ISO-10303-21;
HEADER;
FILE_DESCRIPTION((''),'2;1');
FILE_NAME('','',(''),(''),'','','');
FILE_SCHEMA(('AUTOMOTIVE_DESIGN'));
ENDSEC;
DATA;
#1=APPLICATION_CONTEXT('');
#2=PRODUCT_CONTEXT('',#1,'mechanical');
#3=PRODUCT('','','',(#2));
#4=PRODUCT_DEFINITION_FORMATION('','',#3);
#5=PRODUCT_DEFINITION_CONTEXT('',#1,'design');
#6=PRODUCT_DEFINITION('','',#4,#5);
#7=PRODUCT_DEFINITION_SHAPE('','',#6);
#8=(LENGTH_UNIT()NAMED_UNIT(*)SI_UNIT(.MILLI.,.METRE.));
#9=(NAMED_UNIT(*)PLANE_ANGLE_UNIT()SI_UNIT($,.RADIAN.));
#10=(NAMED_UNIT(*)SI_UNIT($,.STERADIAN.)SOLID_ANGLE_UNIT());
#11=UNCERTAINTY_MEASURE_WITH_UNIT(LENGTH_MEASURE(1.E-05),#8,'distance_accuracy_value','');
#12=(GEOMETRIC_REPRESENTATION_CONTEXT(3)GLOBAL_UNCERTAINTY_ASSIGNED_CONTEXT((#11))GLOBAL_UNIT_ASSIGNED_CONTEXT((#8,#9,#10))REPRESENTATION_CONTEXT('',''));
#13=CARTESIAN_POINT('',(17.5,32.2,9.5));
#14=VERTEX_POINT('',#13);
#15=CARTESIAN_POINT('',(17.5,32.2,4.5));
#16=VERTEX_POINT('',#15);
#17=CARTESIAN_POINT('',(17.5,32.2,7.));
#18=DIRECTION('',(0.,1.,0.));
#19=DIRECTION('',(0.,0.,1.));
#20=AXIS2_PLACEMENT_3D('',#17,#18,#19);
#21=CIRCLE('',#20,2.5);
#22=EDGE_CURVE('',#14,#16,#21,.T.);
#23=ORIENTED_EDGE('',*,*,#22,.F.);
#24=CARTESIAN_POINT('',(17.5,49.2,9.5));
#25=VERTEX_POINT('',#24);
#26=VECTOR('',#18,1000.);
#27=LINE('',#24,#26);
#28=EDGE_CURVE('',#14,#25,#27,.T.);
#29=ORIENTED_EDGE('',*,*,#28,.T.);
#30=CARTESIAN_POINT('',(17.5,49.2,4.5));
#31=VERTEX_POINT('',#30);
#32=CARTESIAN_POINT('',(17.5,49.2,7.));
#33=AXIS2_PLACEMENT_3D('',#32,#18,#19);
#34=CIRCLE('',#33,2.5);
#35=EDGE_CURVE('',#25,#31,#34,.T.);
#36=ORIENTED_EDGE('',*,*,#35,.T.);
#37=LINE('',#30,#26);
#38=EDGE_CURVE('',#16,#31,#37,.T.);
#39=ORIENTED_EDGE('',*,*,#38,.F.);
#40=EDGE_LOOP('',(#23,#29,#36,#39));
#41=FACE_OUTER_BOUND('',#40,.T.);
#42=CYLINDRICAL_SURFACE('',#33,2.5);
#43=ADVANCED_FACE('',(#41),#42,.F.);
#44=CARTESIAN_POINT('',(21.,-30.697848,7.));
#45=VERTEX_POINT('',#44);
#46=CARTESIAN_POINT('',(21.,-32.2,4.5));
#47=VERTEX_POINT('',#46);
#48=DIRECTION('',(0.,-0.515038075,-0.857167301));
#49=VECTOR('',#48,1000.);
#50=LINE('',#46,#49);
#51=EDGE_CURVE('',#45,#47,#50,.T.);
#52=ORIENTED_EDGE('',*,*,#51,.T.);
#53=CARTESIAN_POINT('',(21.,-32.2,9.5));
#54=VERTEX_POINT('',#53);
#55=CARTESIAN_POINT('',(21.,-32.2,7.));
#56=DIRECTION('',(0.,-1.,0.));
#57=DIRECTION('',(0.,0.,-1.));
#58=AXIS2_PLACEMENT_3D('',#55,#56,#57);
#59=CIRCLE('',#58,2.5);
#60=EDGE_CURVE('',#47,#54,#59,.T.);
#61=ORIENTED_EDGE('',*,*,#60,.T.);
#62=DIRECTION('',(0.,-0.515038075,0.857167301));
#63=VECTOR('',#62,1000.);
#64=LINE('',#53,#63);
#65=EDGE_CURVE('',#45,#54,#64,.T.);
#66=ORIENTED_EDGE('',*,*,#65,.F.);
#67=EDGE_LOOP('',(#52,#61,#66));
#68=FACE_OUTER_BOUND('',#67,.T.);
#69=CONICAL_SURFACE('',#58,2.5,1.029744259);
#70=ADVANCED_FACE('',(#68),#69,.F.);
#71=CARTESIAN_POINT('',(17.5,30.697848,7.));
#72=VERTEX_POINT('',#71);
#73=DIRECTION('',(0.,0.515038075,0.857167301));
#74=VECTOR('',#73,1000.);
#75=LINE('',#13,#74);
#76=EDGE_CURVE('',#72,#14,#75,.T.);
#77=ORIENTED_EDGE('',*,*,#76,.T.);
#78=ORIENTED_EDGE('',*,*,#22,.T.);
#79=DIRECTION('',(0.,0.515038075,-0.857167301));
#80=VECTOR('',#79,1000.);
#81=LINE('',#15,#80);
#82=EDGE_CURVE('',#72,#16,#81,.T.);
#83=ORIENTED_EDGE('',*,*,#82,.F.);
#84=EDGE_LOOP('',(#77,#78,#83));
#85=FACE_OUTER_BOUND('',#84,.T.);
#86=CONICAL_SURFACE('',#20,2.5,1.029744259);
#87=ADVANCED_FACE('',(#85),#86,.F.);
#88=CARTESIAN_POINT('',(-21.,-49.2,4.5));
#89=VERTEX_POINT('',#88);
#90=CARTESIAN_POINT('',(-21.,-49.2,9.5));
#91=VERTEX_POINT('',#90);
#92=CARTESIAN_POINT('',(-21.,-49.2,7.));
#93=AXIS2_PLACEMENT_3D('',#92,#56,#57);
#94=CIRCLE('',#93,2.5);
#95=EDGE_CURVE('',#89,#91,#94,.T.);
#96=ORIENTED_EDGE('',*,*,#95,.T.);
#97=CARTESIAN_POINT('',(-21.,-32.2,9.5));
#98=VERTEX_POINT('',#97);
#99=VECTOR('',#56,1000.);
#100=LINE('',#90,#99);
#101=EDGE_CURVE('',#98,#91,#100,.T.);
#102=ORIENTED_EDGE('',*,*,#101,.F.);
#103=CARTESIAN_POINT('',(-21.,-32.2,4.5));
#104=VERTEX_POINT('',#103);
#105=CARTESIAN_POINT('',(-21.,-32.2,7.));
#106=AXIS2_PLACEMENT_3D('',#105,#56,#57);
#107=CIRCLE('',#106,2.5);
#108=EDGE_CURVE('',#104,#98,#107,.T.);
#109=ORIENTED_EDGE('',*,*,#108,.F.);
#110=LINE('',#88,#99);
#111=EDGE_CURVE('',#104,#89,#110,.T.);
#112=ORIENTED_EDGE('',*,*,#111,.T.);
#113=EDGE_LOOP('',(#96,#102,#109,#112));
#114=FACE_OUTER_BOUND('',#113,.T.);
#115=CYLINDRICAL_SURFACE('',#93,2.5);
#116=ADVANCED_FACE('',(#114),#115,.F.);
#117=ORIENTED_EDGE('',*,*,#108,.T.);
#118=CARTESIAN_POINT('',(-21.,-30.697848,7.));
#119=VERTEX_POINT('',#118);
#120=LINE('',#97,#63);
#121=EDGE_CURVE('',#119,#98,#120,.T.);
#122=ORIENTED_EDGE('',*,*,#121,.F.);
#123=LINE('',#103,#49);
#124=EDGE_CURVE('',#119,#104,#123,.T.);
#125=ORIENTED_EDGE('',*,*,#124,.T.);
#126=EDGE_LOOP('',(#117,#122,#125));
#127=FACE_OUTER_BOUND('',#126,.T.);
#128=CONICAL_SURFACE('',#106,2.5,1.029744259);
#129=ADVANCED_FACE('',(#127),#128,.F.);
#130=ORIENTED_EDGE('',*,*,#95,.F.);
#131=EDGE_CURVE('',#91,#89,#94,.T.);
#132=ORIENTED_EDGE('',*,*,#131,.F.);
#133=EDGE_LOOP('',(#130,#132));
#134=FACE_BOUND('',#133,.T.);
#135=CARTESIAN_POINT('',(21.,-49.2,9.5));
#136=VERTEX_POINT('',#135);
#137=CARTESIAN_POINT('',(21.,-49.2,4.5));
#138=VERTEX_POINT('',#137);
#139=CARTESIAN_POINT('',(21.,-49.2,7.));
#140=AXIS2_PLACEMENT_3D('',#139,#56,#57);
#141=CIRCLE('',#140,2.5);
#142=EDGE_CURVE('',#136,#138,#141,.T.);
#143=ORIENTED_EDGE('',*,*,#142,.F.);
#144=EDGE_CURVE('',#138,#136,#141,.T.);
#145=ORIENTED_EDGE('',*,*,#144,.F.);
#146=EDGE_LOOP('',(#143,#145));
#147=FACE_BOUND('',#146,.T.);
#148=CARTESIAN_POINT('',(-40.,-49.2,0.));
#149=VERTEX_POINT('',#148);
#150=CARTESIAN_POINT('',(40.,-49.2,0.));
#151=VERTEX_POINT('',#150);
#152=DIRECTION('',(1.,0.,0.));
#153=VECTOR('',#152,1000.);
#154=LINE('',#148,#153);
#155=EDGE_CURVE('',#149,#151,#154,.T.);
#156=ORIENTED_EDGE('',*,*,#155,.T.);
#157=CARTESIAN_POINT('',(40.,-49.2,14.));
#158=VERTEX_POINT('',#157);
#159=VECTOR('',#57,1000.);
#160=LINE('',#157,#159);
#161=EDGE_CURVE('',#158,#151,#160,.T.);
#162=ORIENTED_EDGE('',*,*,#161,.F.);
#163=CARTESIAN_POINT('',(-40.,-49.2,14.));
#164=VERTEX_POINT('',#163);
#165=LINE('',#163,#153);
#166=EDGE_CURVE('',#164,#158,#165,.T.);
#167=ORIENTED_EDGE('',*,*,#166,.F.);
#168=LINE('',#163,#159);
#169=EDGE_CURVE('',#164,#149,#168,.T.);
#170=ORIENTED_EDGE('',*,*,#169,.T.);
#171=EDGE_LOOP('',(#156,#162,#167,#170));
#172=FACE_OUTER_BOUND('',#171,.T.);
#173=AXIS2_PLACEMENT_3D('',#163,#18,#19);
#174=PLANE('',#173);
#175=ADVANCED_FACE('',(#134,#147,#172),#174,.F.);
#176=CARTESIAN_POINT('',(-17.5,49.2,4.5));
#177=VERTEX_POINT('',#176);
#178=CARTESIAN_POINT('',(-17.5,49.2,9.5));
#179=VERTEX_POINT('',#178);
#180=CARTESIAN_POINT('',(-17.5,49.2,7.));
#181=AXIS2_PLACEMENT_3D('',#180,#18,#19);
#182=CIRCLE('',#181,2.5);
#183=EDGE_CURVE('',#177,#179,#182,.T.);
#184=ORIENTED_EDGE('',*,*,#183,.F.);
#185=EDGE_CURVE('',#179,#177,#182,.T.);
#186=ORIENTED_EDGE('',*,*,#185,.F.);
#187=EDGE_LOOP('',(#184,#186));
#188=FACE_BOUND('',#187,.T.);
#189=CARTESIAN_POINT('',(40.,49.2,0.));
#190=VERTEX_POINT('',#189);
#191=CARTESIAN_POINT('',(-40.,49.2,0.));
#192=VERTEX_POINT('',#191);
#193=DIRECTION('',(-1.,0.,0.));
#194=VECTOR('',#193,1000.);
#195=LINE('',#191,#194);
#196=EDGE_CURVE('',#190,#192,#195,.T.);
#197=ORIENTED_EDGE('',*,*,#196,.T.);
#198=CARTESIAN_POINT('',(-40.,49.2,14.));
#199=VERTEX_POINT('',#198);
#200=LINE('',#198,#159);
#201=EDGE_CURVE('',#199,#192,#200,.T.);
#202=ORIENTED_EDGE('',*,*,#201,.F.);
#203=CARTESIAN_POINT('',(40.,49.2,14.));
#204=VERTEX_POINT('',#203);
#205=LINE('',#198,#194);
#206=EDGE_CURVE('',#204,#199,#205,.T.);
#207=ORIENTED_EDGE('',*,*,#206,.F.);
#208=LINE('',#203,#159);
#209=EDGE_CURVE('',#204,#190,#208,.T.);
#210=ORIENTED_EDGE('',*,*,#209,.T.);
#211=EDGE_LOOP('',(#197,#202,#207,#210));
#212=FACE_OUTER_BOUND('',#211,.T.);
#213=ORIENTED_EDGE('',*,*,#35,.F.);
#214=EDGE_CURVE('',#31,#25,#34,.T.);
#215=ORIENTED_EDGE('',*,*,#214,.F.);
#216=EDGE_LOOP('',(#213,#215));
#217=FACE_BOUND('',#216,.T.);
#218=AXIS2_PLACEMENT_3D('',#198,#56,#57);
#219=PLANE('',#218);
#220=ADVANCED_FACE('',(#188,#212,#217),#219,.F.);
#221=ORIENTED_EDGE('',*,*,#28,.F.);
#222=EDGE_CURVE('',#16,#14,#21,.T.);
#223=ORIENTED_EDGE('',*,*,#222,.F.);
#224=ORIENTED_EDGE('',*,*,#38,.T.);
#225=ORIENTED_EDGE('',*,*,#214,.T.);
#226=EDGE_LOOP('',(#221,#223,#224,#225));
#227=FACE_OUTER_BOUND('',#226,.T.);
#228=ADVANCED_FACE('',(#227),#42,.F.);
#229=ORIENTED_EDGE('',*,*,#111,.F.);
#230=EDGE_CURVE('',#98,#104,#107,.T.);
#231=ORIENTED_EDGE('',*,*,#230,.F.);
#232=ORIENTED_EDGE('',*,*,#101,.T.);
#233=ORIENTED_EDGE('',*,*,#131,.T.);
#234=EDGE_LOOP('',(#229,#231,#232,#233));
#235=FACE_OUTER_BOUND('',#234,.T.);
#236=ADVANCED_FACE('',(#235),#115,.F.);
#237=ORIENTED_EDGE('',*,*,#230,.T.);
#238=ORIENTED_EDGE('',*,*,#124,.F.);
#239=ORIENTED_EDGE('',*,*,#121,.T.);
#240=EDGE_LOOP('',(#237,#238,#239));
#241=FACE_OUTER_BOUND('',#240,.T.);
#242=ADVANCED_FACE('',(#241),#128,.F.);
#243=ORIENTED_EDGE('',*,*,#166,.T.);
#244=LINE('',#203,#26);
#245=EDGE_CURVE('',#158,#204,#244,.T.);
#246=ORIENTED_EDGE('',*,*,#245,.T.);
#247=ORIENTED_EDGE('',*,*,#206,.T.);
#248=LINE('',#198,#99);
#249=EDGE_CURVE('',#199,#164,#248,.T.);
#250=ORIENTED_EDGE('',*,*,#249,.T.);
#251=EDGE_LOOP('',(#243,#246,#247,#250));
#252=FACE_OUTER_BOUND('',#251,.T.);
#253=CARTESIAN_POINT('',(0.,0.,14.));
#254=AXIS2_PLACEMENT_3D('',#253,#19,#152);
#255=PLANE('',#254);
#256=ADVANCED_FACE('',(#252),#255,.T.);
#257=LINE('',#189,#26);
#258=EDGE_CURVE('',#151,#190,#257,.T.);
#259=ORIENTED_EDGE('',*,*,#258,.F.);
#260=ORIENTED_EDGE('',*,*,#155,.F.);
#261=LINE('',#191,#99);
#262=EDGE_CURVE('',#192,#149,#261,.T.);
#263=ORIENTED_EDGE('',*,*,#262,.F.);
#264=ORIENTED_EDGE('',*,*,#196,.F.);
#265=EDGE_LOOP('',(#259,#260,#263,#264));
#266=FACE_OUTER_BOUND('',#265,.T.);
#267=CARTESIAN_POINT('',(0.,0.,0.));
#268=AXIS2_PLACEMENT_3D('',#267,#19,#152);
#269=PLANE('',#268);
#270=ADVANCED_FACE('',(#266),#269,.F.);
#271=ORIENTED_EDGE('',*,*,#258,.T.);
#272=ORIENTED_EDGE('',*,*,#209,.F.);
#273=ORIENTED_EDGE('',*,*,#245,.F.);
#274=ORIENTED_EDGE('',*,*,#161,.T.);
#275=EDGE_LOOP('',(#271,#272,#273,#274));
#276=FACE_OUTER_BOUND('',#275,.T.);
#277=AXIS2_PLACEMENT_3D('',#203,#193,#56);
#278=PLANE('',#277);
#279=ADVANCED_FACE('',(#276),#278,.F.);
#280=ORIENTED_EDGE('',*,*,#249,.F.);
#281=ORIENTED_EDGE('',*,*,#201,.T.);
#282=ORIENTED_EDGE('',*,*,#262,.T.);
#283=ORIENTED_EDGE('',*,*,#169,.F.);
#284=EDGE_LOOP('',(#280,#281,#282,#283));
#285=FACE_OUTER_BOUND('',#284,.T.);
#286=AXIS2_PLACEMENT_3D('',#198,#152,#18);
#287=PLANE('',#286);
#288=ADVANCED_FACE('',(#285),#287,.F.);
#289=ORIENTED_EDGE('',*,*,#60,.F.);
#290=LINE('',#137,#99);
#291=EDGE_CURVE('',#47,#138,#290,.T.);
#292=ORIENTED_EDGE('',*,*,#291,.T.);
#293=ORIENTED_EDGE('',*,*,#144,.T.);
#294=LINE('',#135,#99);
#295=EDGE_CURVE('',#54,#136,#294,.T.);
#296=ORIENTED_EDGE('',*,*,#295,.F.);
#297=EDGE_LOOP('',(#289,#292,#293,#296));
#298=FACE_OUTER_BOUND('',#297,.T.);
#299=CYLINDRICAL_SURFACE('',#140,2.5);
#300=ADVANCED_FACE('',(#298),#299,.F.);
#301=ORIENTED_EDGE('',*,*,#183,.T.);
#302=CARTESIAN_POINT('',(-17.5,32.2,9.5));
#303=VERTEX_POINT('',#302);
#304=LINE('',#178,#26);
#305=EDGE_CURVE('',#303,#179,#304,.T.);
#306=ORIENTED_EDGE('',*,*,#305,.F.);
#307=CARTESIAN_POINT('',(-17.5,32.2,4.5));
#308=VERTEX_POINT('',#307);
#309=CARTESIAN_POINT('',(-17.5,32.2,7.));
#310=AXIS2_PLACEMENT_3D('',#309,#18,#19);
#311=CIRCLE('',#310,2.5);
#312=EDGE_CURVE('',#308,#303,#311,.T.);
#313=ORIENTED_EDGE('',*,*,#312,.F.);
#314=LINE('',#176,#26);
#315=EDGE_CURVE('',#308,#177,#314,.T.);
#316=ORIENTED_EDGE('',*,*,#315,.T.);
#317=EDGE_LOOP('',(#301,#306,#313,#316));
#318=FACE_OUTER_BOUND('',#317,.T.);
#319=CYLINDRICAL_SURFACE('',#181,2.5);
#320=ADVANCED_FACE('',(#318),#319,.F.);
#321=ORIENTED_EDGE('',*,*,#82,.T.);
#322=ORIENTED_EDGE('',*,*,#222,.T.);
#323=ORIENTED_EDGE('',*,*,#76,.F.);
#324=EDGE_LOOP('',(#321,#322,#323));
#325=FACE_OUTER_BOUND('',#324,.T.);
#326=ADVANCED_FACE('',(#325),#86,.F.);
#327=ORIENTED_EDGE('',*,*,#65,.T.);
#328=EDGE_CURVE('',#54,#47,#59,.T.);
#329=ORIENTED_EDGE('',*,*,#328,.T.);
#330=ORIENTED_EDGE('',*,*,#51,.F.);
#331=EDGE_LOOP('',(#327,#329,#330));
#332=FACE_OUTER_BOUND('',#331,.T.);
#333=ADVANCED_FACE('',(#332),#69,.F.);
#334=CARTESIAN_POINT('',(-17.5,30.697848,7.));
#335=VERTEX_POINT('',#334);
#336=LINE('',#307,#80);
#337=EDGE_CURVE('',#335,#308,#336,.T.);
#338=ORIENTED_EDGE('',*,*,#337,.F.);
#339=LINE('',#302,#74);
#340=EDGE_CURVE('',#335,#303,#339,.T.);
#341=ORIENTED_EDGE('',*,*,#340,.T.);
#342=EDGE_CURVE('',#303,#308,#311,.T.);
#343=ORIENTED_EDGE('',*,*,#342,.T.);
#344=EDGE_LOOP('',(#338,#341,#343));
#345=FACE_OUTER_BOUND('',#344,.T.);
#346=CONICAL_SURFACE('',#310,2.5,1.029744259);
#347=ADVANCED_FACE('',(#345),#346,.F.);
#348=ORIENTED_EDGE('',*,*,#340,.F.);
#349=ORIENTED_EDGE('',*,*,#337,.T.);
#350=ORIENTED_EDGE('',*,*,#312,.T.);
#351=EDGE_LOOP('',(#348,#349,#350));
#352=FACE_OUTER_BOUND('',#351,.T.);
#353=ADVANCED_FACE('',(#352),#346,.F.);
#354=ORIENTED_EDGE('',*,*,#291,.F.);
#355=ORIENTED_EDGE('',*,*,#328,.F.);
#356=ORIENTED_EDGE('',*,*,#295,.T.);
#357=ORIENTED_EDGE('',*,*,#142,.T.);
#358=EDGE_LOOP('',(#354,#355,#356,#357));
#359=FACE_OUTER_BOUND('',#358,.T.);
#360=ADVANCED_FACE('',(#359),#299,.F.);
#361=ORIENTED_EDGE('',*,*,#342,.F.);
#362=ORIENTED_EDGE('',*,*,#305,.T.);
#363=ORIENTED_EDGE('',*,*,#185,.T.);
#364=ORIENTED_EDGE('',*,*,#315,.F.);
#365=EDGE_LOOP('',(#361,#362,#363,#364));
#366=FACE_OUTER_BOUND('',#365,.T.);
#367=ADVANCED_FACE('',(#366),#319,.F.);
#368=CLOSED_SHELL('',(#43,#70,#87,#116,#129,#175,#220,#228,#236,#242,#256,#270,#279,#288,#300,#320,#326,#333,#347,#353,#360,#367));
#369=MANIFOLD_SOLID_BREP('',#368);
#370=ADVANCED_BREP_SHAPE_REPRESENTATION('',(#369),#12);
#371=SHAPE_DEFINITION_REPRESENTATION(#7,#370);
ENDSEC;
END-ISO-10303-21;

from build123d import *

# Parameters (mm, degrees)
SKETCH_1_W             = 80
SKETCH_1_H             = 98.4
EXTRUDE_1_DEPTH        = 14
HOLE_WIZARD_M6_1_D     = 5
HOLE_WIZARD_M6_1_DEPTH = 17
HOLE_WIZARD_M6_1_TIP   = 1.502151548
HOLE_WIZARD_M6_2_D     = 5
HOLE_WIZARD_M6_2_DEPTH = 17
HOLE_WIZARD_M6_2_TIP   = 1.502151548


with BuildPart() as part:
    # 草图1 → 凸台-拉伸1 (new body)
    with BuildSketch(Plane.XY):
        Rectangle(SKETCH_1_W, SKETCH_1_H)
    extrude(amount=EXTRUDE_1_DEPTH)

    # M6 螺纹孔1
    with Locations(Plane(origin=(0, -49.2, 0), x_dir=(-1, 0, 0), z_dir=(0, -1, 0))):
        with Locations((-21, -7), (21, -7)):
            Hole(HOLE_WIZARD_M6_1_D / 2, depth=HOLE_WIZARD_M6_1_DEPTH)
            with Locations((0, 0, -(HOLE_WIZARD_M6_1_DEPTH + HOLE_WIZARD_M6_1_TIP / 2))):  # 118° drill point
                Cone(0, HOLE_WIZARD_M6_1_D / 2, HOLE_WIZARD_M6_1_TIP, mode=Mode.SUBTRACT)

    # M6 螺纹孔2
    with Locations(Plane(origin=(0, 49.2, 0), x_dir=(1, 0, 0), z_dir=(0, 1, 0))):
        with Locations((-17.5, -7), (17.5, -7)):
            Hole(HOLE_WIZARD_M6_2_D / 2, depth=HOLE_WIZARD_M6_2_DEPTH)
            with Locations((0, 0, -(HOLE_WIZARD_M6_2_DEPTH + HOLE_WIZARD_M6_2_TIP / 2))):  # 118° drill point
                Cone(0, HOLE_WIZARD_M6_2_D / 2, HOLE_WIZARD_M6_2_TIP, mode=Mode.SUBTRACT)


solid = part.part
